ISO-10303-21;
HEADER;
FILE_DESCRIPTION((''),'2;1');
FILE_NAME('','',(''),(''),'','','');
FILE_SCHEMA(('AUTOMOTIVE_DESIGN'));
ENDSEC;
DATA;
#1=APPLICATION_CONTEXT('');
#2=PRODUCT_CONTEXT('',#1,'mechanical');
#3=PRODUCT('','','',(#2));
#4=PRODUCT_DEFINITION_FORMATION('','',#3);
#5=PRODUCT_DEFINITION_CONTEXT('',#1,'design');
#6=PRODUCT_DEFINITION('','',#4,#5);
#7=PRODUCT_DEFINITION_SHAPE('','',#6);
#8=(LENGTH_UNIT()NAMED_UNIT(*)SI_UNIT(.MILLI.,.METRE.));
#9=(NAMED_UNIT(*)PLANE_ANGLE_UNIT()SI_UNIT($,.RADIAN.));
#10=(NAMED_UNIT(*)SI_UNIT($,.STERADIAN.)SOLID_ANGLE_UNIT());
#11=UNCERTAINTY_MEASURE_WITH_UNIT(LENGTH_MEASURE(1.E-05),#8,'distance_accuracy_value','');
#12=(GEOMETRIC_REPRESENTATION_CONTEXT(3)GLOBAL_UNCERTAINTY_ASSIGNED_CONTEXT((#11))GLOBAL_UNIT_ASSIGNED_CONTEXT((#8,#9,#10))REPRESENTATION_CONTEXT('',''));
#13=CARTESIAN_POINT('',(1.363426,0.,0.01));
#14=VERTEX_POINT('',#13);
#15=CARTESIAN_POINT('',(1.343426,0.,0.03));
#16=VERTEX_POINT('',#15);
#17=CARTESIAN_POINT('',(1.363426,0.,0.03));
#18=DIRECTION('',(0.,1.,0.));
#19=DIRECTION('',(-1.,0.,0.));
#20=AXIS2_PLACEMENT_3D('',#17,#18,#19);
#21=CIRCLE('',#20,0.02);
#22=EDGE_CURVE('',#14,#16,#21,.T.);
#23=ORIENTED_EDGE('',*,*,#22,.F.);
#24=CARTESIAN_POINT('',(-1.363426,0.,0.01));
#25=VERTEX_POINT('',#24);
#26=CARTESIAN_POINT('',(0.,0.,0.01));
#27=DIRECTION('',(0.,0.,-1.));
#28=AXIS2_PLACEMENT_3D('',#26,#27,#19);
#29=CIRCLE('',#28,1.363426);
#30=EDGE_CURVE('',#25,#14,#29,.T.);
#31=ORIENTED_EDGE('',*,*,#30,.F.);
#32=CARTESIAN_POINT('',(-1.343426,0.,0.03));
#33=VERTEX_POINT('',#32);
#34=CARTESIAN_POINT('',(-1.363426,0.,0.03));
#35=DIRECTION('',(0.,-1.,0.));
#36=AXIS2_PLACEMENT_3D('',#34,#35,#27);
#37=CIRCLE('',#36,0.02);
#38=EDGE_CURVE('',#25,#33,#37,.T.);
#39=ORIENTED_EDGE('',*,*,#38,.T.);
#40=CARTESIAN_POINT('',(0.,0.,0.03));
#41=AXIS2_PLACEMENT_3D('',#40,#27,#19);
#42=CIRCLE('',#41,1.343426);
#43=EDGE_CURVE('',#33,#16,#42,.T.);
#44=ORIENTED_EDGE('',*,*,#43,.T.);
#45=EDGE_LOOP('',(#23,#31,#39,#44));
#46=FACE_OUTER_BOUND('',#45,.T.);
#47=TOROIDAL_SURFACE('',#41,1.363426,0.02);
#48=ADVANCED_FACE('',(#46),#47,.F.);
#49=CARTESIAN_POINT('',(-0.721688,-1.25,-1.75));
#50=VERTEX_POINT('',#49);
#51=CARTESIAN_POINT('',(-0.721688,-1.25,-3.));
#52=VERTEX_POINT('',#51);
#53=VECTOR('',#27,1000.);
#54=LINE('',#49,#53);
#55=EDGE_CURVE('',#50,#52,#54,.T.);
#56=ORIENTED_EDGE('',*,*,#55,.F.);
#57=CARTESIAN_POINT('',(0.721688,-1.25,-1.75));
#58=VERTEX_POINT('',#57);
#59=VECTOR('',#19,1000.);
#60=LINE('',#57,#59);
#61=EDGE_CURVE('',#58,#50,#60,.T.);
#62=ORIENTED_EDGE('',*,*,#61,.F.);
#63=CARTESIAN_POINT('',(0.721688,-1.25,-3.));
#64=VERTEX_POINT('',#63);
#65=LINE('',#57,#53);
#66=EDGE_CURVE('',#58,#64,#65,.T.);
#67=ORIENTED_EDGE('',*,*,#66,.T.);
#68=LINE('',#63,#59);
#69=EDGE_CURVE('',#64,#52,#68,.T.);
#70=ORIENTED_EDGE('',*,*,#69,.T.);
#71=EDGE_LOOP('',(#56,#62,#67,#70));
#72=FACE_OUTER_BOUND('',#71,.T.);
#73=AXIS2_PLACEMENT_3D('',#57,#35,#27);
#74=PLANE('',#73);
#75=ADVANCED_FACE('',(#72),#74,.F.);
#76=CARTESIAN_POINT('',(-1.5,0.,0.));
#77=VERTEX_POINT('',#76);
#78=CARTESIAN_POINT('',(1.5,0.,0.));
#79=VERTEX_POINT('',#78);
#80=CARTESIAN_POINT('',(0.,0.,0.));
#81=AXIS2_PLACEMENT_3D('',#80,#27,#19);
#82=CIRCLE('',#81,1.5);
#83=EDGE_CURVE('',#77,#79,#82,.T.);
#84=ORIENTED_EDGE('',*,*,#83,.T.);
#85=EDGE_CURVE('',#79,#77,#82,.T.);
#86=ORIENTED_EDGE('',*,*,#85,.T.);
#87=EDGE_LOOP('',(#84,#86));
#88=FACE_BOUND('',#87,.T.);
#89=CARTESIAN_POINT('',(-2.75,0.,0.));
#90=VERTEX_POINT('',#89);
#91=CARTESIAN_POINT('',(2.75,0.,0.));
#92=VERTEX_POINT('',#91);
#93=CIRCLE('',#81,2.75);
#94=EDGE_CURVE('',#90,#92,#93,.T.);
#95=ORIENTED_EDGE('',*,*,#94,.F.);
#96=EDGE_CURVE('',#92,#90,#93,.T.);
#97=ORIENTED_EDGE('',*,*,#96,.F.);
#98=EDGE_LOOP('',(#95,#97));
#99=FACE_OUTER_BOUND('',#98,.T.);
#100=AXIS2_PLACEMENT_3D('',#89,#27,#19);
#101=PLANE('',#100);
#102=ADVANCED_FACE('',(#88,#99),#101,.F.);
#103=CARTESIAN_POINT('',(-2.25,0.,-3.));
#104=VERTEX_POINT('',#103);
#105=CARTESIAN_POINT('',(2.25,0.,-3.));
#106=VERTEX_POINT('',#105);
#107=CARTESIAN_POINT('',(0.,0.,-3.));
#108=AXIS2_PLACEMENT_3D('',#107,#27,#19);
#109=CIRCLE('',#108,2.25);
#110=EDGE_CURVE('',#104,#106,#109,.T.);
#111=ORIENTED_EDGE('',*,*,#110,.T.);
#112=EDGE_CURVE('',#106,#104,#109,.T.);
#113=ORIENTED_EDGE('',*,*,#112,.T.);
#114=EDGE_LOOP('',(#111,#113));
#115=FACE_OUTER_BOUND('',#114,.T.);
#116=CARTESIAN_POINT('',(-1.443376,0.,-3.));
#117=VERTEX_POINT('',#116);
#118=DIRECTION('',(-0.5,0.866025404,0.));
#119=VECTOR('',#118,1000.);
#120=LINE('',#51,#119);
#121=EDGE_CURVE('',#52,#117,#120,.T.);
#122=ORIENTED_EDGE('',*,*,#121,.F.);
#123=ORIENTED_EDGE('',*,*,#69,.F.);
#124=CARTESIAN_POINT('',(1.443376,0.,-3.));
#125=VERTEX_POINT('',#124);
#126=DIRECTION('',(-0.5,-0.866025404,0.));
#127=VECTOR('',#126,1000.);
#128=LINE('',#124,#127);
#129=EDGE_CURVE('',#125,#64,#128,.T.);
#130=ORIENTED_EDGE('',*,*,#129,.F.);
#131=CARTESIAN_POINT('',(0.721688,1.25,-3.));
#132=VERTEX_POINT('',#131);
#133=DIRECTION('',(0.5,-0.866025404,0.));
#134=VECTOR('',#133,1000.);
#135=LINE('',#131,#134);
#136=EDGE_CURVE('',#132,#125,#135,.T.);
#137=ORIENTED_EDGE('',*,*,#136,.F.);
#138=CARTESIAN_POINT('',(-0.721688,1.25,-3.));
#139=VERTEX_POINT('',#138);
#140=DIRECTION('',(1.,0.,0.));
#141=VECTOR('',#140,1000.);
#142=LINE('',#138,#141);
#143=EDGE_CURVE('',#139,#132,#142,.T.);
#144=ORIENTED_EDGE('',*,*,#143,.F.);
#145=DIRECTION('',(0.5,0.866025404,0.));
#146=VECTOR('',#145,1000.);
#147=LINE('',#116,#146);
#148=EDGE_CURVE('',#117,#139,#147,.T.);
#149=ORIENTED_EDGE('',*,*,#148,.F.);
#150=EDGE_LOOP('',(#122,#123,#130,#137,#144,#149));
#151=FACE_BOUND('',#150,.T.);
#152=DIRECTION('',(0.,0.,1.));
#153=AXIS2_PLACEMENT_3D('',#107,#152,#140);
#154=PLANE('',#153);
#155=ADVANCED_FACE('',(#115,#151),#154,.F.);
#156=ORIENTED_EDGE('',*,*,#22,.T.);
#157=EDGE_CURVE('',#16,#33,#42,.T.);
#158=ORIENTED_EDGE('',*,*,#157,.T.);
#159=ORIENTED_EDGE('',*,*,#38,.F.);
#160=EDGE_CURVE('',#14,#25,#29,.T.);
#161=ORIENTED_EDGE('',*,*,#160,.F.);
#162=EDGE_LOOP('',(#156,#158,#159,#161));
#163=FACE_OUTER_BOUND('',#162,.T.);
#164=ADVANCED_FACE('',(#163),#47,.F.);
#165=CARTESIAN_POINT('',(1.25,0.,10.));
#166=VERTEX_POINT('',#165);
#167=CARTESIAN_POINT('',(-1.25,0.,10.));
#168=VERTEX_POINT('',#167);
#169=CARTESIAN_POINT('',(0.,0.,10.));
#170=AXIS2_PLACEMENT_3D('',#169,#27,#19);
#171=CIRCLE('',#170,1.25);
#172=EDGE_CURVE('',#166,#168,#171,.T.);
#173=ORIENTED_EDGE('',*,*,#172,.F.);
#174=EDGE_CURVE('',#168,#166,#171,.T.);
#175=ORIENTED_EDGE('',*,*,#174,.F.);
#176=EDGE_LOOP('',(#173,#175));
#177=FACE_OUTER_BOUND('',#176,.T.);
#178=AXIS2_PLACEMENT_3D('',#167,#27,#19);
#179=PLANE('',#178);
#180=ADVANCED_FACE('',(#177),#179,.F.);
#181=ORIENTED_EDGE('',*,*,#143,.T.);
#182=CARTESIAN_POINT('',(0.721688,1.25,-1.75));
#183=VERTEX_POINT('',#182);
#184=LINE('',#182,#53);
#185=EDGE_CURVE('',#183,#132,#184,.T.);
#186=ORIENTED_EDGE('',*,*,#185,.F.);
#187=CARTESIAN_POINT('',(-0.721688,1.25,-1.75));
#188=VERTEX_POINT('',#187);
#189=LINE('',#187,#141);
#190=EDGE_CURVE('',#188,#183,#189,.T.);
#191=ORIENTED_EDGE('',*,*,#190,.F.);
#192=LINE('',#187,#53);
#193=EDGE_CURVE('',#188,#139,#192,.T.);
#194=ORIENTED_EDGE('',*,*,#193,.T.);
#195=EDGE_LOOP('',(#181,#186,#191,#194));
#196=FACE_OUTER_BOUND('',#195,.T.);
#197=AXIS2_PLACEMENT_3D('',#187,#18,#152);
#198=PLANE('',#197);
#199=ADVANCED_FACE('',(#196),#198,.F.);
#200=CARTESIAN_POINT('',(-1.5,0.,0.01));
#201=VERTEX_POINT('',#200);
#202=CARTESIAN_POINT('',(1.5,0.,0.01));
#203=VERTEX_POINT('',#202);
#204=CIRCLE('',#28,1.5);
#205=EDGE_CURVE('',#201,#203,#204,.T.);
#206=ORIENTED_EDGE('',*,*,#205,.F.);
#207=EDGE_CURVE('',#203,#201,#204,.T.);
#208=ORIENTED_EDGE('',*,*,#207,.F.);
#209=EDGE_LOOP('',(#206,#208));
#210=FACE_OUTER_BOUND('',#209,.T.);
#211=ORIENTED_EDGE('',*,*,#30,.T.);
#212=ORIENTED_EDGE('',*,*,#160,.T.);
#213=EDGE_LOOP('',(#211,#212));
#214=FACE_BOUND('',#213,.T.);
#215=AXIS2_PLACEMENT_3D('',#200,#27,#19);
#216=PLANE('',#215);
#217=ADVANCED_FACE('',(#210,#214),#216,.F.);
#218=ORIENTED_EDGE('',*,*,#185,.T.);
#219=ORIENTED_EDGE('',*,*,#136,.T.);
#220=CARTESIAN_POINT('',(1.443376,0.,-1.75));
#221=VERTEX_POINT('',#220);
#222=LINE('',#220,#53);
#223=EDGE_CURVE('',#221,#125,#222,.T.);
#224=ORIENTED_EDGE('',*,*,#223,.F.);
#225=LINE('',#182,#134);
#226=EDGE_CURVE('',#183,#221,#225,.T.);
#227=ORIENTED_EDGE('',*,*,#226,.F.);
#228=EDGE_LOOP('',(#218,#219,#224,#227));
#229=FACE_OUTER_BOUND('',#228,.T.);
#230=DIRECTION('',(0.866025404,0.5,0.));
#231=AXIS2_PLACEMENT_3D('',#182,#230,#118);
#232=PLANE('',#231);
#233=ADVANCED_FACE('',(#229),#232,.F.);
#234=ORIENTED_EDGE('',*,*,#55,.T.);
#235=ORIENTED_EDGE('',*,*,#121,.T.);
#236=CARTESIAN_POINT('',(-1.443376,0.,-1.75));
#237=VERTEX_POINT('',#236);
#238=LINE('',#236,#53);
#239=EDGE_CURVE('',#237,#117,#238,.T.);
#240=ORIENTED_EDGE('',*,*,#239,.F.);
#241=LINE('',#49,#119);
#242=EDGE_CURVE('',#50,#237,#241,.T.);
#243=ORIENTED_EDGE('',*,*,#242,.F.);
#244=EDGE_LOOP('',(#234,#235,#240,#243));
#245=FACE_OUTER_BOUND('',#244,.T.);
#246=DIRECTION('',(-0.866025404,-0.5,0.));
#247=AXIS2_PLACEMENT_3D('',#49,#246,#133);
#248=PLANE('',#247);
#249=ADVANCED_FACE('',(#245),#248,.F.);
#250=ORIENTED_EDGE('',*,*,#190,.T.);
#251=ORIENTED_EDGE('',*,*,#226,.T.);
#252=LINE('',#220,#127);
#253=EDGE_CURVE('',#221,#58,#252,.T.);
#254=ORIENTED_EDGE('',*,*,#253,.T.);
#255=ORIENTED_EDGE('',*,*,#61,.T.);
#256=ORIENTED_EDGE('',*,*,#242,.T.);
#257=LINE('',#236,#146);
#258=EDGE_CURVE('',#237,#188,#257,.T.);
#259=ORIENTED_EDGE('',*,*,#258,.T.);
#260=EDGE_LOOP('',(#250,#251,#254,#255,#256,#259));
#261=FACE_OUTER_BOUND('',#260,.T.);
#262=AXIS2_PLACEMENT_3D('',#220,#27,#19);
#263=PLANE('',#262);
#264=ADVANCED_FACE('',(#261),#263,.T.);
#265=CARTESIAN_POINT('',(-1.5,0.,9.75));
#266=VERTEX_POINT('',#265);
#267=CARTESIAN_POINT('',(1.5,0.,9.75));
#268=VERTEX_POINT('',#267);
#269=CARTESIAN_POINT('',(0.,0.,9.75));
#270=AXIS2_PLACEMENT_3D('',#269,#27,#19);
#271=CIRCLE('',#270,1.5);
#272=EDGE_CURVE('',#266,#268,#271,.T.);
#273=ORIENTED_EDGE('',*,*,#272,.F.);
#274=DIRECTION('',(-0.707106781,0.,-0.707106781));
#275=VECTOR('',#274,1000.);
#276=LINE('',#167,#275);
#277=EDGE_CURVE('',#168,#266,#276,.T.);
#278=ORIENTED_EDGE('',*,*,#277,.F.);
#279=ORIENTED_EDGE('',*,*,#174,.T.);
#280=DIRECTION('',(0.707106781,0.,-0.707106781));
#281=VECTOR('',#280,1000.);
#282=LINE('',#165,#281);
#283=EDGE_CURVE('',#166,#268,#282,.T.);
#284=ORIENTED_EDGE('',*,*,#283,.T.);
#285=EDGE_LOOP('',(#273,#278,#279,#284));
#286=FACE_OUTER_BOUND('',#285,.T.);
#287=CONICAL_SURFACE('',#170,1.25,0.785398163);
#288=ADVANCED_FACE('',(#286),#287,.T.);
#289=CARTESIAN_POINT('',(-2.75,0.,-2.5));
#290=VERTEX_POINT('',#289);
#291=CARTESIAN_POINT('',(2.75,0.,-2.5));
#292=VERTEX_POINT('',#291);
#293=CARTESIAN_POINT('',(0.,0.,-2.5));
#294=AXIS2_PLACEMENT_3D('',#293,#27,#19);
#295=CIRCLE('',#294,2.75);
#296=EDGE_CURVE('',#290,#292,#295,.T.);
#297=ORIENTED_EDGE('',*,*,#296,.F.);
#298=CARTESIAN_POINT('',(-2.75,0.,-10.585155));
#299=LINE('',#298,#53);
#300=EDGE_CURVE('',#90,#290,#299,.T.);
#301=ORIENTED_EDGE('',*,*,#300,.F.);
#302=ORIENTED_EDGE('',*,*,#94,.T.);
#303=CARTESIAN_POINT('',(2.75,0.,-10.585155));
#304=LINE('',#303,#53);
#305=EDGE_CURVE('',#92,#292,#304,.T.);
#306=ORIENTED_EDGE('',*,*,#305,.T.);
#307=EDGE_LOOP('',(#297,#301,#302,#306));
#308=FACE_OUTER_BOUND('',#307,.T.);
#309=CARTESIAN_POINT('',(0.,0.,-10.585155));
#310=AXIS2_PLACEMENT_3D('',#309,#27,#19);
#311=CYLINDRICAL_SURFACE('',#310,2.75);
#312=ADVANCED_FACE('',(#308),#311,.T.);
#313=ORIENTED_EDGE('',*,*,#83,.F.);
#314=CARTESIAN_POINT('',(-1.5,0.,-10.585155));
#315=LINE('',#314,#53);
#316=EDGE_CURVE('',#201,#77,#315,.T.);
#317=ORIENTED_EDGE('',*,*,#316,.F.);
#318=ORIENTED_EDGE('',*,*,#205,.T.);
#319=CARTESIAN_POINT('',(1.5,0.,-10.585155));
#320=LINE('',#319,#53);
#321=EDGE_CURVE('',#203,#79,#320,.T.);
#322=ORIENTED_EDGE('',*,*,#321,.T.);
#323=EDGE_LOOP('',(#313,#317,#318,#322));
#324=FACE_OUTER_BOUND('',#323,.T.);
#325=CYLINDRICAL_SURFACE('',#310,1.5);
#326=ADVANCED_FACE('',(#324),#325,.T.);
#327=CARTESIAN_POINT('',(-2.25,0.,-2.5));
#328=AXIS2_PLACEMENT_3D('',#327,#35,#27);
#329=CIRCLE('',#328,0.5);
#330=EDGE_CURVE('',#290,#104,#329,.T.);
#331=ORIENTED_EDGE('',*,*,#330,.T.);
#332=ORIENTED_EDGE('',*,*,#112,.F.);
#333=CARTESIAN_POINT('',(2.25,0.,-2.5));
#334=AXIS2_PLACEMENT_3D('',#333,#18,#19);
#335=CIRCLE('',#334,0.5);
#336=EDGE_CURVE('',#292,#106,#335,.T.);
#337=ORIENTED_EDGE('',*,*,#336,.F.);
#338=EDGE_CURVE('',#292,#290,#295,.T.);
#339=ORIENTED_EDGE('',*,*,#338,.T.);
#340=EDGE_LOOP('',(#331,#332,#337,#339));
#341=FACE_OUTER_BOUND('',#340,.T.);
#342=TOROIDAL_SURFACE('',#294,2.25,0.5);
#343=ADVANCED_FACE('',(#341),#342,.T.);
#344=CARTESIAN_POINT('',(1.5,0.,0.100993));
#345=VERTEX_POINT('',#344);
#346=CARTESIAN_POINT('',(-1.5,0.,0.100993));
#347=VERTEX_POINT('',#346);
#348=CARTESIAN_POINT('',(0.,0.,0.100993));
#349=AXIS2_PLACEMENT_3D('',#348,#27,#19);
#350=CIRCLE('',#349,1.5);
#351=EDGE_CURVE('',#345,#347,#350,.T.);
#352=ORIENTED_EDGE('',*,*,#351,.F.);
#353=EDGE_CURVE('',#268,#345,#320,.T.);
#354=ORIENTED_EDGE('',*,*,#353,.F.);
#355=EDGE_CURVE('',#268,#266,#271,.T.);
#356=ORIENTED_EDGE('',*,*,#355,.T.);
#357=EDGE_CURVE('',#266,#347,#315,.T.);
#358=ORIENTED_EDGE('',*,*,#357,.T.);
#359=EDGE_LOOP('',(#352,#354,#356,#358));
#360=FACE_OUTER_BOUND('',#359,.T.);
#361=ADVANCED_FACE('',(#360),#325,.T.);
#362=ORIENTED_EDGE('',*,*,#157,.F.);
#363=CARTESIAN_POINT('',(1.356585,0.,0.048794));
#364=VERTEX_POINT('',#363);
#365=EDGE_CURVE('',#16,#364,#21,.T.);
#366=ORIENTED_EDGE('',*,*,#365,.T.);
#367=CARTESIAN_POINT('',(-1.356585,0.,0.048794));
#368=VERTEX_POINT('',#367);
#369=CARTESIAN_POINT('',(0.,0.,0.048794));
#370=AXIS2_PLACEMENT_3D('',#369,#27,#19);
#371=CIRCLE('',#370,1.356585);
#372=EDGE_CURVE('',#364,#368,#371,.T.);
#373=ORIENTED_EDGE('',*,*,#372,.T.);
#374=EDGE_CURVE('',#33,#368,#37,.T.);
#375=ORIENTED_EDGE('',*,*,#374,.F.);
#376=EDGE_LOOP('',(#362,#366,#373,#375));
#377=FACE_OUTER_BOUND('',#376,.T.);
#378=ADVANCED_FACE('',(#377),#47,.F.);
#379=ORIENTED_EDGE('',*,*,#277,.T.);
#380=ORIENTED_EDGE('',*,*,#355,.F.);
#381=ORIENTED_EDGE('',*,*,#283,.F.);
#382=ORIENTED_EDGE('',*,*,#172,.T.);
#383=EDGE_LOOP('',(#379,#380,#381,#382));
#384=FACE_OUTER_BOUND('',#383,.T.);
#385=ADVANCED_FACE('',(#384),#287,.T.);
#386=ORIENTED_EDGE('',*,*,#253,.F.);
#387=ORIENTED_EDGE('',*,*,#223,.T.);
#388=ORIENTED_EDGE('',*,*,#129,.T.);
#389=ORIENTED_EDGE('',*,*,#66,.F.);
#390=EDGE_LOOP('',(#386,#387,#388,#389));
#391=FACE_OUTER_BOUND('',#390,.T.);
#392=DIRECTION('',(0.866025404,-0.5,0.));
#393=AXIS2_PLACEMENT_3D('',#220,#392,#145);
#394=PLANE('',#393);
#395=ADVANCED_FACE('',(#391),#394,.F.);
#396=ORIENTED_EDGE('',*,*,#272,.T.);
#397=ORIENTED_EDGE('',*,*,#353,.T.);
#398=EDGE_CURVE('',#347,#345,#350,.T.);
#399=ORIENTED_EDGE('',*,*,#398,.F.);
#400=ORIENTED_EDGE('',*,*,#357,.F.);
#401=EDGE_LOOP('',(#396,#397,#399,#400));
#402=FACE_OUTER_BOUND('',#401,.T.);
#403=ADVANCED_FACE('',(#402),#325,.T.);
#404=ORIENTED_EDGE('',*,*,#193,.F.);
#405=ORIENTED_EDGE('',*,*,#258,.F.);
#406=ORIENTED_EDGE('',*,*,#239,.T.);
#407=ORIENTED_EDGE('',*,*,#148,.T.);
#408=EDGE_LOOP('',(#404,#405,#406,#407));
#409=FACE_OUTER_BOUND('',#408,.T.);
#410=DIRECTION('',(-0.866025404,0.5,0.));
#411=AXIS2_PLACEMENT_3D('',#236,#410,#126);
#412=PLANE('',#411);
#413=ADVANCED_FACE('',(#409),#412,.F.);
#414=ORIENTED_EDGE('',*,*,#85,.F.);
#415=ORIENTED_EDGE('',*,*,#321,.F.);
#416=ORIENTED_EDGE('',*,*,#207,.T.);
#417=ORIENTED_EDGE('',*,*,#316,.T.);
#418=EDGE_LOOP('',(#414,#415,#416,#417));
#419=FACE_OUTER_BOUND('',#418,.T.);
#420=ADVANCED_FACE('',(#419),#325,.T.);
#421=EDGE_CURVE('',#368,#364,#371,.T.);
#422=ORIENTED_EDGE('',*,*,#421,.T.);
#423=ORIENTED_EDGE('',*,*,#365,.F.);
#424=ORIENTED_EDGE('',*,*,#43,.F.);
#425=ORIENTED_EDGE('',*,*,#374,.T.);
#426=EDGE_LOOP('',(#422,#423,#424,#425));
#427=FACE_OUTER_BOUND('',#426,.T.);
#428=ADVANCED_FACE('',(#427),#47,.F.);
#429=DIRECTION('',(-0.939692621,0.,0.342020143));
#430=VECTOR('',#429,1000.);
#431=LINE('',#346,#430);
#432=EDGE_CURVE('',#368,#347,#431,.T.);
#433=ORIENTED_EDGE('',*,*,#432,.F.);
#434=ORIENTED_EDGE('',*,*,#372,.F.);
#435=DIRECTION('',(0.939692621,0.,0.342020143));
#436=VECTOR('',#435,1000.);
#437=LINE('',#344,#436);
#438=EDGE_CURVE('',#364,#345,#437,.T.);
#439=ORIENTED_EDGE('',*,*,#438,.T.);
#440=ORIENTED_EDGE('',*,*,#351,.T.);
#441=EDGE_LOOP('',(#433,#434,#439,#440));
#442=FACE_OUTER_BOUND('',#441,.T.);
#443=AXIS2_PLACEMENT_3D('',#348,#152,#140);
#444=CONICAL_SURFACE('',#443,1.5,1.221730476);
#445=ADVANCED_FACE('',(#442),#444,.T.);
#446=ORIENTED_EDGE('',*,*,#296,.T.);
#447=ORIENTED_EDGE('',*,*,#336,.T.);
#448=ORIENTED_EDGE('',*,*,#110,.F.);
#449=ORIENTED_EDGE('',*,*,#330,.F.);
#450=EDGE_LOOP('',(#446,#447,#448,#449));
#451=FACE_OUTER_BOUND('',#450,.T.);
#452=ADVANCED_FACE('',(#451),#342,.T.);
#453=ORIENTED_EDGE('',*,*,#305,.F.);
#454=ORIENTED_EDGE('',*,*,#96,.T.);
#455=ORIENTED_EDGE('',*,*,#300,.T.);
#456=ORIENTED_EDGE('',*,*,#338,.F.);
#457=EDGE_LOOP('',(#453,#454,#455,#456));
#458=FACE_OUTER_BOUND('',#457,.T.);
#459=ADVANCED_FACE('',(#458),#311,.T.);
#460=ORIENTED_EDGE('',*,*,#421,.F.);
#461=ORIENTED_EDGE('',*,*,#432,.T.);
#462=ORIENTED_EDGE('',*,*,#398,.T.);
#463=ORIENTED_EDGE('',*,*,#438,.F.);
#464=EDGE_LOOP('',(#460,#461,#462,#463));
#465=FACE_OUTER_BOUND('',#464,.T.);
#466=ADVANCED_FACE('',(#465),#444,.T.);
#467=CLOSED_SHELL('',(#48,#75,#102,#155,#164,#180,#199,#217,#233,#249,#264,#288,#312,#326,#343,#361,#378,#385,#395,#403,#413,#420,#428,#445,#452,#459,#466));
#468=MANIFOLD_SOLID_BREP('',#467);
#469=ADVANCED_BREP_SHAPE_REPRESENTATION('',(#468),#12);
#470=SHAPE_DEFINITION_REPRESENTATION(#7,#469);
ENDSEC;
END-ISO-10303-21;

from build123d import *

# Parameters (mm, degrees)
CUT_EXTRUDE1_DEPTH = 1.25


with BuildPart() as part:
    # Logo3_bib1 → Revolve1 (revolve)
    with BuildSketch(Plane(origin=(0, 0, 0), x_dir=(-1, 0, 0), z_dir=(0, -1, 0))):
        with BuildLine():
            Line((0, -10), (0, 3))
            Line((0, 3), (2.25, 3))
            ThreePointArc((2.25, 3), (2.603553391, 2.853553391), (2.75, 2.5))
            Line((2.75, 2.5), (2.75, 0))
            Line((2.75, 0), (1.5, 0))
            Line((1.5, 0), (1.5, -0.01))
            Line((1.5, -0.01), (1.363425636, -0.01))
            ThreePointArc((1.363425636, -0.01), (1.343729481, -0.026527036), (1.356585234, -0.048793852))
            Line((1.356585234, -0.048793852), (1.5, -0.100992559))
            Line((1.5, -0.100992559), (1.5, -9.75))
            Line((1.5, -9.75), (1.25, -10))
            Line((1.25, -10), (0, -10))
        make_face()
    revolve(axis=Axis((0, 0, -10.585154653), (0, 0, 1)))

    # Logo3_bib2 → Cut-Extrude1 (cut)
    with BuildSketch(Plane(origin=(0, 0, -3), x_dir=(1, 0, 0), z_dir=(0, 0, -1))):
        Polygon((1.443375673, 0), (0.721687836, 1.25), (-0.721687836, 1.25), (-1.443375673, 0), (-0.721687836, -1.25), (0.721687836, -1.25), align=None)
    extrude(amount=-CUT_EXTRUDE1_DEPTH, mode=Mode.SUBTRACT)


solid = part.part
